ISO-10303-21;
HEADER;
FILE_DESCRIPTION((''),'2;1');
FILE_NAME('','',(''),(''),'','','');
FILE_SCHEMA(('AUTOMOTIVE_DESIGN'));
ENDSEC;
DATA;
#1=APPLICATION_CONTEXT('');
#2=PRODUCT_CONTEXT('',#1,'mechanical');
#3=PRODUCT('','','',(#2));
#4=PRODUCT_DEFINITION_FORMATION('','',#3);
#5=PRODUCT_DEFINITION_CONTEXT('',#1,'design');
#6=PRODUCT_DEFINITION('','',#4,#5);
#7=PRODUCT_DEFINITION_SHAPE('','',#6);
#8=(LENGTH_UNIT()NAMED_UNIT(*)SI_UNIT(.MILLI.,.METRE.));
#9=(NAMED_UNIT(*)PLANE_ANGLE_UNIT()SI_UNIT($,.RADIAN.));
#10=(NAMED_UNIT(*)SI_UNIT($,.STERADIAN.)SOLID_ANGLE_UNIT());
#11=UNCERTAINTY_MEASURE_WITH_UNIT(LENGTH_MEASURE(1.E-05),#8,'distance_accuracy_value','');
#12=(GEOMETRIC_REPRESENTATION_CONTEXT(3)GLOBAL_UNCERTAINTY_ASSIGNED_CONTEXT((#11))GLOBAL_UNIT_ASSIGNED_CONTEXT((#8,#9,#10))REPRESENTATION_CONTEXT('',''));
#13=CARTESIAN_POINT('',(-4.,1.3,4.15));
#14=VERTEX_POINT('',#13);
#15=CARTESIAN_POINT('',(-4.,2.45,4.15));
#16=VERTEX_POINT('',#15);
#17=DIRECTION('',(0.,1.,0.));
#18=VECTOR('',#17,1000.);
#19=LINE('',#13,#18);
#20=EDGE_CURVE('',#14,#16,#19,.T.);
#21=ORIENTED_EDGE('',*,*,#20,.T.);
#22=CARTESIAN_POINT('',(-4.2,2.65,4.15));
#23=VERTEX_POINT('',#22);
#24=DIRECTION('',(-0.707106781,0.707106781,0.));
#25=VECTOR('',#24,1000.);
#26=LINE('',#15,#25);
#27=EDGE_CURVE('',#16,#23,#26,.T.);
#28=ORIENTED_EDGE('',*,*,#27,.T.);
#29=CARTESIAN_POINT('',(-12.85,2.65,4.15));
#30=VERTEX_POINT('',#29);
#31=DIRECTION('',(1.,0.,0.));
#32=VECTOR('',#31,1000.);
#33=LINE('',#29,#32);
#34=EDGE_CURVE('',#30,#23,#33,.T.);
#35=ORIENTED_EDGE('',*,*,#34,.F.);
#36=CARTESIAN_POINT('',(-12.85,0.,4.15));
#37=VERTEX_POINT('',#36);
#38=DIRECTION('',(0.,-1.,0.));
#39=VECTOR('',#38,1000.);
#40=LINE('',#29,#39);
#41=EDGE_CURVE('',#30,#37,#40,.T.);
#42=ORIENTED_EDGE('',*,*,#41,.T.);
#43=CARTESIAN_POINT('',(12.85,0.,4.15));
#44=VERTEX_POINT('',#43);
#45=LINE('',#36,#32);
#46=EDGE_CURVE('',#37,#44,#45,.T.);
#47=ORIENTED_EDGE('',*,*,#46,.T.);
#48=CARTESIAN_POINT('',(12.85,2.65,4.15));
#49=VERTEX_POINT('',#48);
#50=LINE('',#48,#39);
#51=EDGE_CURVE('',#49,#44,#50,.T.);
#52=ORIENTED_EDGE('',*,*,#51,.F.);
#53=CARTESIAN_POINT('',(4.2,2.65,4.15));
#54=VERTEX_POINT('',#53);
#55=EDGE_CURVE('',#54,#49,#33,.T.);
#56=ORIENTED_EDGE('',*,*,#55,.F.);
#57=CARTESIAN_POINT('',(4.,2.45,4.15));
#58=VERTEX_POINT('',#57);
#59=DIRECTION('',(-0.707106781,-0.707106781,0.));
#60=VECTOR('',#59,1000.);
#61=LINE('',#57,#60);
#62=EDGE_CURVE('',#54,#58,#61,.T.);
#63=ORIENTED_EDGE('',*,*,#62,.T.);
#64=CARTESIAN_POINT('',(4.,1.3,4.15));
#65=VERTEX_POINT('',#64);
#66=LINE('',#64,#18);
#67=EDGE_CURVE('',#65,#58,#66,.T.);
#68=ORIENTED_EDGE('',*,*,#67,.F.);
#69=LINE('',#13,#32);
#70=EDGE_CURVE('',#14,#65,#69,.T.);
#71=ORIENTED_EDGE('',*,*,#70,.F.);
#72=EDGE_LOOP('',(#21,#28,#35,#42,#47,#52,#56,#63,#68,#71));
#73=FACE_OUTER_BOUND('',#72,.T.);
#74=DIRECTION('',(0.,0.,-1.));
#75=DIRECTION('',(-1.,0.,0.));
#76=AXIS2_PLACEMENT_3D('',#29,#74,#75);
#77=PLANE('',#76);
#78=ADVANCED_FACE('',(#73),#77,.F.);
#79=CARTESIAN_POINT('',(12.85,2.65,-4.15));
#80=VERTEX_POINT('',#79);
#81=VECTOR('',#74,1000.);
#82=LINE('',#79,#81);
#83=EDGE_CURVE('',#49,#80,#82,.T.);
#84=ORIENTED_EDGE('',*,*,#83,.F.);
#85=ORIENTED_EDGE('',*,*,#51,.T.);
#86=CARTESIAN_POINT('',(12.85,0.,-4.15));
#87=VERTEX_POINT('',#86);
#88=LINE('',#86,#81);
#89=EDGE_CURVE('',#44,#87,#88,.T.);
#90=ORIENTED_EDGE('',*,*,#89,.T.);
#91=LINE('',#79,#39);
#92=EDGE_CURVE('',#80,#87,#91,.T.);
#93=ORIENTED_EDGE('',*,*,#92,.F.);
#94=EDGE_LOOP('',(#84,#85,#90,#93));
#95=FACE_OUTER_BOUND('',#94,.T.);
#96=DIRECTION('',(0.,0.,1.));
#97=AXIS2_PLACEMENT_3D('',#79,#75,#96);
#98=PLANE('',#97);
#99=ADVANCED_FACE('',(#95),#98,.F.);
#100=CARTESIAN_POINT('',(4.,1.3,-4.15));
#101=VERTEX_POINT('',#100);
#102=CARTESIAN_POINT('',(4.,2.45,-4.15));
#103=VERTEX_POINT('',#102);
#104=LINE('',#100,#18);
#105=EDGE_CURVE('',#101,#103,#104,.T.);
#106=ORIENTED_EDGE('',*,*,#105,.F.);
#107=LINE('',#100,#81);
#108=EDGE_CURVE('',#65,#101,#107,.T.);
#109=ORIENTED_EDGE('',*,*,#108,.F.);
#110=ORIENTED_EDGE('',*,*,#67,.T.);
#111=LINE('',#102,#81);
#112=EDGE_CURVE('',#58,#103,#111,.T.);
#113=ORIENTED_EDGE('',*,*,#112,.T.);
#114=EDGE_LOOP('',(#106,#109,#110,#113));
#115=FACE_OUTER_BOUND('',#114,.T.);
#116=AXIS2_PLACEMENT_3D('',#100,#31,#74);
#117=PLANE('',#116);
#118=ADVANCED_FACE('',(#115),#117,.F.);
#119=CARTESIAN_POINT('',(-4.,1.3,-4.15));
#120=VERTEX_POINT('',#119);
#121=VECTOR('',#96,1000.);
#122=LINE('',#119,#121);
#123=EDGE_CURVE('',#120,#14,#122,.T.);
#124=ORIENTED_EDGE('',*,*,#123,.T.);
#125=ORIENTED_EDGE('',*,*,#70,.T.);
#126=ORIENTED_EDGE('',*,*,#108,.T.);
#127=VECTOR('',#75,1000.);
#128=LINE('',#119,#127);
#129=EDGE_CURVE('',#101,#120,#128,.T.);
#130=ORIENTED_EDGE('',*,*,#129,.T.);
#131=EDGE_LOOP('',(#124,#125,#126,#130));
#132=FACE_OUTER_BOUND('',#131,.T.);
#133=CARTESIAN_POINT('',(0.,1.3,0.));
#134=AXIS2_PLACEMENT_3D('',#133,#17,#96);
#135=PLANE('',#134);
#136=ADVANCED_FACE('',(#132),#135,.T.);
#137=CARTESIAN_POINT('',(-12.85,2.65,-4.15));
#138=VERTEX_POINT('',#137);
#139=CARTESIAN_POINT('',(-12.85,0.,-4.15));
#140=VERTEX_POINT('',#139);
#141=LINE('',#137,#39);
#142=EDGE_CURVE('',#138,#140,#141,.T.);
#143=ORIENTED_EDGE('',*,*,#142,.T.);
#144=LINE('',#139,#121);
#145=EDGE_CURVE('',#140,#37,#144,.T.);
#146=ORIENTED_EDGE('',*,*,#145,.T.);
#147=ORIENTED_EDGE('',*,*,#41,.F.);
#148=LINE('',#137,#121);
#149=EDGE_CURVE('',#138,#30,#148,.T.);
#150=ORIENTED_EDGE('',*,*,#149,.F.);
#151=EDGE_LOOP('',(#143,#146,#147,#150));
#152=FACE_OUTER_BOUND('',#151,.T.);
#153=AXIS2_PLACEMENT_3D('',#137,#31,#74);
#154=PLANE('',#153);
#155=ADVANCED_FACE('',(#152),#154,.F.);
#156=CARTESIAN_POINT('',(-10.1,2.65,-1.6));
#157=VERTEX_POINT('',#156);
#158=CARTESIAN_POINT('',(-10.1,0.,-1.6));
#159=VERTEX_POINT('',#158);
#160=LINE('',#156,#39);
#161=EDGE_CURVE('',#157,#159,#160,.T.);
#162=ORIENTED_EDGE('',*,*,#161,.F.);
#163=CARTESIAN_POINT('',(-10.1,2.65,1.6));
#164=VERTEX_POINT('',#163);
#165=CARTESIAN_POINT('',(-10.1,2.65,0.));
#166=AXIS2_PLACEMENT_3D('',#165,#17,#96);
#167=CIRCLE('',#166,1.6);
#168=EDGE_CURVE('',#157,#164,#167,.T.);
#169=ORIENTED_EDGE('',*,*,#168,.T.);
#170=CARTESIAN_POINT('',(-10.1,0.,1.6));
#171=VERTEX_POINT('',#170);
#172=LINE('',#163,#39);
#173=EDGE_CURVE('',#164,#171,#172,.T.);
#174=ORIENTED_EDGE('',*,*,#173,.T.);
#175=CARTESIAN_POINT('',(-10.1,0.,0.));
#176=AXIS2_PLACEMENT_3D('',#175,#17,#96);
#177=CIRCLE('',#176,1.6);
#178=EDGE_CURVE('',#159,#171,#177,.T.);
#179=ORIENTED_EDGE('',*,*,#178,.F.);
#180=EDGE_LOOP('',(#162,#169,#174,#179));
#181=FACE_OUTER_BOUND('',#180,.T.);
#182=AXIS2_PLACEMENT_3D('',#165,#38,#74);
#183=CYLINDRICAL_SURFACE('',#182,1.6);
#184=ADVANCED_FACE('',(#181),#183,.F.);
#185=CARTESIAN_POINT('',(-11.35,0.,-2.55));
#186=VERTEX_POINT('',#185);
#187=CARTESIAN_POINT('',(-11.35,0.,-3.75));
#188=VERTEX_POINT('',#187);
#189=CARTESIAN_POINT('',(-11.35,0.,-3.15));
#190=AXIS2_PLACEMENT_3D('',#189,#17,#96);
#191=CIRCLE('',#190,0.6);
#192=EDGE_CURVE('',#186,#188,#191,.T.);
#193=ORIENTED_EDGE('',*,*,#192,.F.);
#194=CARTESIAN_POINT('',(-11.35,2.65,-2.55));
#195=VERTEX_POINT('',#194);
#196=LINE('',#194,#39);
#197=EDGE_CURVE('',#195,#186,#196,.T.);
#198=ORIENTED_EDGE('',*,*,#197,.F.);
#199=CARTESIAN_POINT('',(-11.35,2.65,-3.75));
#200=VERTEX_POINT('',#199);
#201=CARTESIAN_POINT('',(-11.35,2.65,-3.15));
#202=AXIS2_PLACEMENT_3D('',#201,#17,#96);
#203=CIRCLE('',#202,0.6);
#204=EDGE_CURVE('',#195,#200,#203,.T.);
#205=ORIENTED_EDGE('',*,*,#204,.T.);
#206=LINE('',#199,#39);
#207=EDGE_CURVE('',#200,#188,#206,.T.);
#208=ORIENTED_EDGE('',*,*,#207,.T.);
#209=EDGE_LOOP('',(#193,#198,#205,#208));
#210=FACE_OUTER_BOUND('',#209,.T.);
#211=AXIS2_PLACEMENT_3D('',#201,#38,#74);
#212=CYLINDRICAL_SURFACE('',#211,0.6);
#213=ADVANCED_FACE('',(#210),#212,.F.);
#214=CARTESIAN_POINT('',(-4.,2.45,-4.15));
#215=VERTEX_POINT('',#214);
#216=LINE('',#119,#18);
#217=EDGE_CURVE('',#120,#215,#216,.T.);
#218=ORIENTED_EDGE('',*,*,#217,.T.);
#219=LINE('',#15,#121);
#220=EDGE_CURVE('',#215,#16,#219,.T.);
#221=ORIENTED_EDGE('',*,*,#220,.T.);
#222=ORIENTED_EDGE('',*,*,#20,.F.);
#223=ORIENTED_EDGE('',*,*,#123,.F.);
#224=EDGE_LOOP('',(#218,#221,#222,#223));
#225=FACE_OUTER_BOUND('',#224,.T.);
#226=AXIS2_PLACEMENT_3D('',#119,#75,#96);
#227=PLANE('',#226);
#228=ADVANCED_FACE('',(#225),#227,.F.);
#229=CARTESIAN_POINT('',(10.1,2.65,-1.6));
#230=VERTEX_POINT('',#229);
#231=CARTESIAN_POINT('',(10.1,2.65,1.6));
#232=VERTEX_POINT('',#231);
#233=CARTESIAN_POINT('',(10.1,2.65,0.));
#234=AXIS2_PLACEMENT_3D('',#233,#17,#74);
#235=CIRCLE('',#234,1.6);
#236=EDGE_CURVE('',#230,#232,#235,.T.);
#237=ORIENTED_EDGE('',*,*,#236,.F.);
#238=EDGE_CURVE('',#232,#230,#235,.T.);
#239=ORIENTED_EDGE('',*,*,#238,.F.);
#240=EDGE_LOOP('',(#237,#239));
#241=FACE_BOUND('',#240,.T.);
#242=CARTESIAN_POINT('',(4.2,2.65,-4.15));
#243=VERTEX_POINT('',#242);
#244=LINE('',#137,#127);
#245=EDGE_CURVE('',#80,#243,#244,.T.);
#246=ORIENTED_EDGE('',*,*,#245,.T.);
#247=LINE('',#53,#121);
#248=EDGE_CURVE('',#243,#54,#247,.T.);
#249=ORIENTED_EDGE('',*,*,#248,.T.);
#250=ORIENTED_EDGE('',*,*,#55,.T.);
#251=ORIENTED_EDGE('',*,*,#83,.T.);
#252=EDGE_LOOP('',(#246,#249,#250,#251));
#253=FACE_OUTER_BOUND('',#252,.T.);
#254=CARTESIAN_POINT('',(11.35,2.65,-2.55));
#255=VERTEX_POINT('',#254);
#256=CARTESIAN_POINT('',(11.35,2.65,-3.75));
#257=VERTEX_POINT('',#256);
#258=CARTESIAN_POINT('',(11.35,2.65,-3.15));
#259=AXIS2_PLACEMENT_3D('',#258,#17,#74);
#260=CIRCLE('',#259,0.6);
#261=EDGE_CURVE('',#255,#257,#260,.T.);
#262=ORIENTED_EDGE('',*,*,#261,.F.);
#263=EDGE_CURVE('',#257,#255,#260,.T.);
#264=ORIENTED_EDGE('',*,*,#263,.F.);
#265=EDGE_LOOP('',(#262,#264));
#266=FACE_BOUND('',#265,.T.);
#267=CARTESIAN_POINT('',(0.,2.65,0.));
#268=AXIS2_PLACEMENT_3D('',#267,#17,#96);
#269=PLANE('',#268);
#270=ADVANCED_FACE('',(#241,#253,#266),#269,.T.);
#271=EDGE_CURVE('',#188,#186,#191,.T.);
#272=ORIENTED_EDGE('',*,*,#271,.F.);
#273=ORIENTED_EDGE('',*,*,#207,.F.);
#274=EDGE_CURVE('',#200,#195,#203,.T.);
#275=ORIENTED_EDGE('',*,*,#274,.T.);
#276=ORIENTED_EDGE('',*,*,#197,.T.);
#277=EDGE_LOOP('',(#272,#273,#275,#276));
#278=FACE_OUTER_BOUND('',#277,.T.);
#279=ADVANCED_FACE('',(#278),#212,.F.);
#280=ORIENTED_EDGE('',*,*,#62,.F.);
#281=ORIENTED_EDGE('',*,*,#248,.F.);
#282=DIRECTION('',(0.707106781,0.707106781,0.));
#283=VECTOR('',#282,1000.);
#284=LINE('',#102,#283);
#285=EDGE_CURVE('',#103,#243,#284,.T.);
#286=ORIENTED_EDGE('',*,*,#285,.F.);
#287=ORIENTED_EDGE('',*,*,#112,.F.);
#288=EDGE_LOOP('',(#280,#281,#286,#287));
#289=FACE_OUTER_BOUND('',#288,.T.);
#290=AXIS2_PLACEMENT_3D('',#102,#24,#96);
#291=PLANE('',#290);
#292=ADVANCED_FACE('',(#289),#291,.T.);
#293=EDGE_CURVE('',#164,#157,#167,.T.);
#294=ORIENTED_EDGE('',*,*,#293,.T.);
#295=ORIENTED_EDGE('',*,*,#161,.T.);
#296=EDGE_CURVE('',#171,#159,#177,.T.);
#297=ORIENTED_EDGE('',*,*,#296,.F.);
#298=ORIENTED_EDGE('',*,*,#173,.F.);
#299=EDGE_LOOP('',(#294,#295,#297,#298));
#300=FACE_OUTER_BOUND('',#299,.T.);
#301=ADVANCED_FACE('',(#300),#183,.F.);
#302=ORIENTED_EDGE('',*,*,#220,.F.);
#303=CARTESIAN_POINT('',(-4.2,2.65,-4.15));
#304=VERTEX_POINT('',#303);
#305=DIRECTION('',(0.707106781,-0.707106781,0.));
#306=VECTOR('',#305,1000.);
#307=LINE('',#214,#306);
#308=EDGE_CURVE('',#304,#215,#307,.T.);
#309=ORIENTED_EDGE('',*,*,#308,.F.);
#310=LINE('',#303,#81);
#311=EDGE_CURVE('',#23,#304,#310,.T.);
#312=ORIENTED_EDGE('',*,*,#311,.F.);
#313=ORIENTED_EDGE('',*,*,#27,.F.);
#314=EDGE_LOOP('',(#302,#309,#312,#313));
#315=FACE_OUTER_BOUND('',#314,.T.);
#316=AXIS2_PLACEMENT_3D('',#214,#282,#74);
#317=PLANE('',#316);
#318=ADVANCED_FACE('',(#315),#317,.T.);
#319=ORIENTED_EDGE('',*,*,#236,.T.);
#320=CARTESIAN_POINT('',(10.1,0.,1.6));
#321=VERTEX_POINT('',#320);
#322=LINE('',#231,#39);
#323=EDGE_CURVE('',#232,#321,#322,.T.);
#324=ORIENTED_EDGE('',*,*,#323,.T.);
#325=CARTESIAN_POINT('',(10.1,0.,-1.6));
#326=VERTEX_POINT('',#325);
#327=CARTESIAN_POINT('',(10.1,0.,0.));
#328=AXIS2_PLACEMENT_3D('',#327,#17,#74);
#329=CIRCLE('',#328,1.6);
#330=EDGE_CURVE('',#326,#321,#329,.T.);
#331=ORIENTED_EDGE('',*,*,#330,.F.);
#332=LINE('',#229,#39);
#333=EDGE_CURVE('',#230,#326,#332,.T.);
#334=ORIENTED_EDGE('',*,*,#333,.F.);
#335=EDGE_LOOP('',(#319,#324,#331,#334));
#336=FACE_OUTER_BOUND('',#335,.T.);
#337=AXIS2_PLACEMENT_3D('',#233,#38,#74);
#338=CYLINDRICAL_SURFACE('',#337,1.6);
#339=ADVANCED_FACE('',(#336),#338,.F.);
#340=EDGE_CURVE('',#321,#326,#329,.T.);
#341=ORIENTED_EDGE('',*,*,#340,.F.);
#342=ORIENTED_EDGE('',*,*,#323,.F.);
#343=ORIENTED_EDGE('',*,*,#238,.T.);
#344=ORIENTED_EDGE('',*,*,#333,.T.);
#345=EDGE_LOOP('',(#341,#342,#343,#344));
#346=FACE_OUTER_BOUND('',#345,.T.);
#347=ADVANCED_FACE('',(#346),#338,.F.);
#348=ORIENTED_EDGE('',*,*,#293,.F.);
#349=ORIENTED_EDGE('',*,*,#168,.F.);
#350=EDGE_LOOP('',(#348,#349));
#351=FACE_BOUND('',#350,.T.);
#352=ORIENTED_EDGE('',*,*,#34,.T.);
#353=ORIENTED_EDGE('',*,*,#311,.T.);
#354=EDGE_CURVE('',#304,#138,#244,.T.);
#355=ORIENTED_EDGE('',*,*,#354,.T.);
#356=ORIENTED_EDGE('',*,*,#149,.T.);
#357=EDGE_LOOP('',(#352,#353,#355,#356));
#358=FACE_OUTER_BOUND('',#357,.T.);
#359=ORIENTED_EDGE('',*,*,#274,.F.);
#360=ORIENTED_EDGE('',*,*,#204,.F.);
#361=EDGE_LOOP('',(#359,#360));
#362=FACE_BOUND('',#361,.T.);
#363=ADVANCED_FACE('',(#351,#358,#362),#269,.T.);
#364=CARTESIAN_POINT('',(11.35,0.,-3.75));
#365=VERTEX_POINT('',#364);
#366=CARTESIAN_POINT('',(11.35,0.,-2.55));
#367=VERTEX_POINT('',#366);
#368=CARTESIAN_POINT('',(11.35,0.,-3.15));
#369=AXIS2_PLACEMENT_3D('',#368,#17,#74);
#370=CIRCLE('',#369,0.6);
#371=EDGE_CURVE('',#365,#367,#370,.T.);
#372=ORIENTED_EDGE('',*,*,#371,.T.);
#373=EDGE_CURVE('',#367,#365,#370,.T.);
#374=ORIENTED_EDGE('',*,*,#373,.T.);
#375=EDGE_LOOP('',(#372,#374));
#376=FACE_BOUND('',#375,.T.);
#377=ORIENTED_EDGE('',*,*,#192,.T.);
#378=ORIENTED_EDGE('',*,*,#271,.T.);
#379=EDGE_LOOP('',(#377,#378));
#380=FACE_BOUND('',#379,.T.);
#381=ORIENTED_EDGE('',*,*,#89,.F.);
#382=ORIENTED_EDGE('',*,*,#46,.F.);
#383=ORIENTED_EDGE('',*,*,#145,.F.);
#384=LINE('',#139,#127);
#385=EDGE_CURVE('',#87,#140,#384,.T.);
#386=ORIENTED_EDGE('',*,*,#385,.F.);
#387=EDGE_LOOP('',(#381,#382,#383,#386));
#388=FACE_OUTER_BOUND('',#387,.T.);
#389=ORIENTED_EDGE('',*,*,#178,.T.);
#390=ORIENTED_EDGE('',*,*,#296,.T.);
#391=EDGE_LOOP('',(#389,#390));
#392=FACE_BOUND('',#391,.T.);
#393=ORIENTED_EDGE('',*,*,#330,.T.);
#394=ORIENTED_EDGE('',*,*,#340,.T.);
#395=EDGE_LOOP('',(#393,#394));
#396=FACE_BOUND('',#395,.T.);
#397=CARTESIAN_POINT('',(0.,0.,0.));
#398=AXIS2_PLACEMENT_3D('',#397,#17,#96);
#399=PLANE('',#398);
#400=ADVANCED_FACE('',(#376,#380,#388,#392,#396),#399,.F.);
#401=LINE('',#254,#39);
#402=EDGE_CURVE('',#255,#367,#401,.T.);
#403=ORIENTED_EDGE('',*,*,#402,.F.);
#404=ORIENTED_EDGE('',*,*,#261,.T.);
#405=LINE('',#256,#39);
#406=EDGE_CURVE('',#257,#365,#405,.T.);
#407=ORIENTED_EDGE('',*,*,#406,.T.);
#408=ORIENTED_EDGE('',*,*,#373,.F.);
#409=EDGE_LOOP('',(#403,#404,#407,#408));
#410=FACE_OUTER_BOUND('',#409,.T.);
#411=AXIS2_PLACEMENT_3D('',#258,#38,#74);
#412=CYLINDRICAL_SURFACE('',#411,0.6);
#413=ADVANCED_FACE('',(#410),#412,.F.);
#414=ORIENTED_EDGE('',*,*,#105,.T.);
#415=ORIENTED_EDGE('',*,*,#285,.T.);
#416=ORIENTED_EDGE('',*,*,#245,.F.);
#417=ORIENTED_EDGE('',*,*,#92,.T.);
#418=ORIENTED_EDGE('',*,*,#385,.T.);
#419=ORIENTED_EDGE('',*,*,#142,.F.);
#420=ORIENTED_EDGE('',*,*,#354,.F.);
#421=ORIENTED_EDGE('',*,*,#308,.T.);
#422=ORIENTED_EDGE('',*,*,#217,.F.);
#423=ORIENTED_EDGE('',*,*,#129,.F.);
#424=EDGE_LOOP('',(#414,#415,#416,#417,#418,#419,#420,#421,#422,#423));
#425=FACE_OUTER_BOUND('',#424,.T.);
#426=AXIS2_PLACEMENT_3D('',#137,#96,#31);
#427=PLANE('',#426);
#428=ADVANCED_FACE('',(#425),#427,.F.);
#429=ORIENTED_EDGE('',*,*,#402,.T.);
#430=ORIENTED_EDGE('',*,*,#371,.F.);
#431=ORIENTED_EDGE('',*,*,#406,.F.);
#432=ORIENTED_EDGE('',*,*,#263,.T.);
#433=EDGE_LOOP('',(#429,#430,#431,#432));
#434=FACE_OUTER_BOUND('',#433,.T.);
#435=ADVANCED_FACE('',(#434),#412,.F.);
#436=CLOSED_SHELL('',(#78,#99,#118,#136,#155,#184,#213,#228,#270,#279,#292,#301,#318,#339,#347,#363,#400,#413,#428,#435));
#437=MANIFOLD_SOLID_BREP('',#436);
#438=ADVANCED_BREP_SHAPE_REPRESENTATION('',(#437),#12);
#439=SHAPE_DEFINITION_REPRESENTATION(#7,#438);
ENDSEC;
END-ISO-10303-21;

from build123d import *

# Parameters (mm, degrees)
SKETCH1_W           = 25.7
SKETCH1_H           = 8.3
SKETCH1_R           = 1.6
SKETCH1_R_2         = 0.6
BOSS_EXTRUDE1_DEPTH = 2.65
SKETCH2_W           = 8
SKETCH2_H           = 8.3
CUT_EXTRUDE1_DEPTH  = 1.35
CHAMFER1_SIZE       = 0.2


with BuildPart() as part:
    # Sketch1 → Boss-Extrude1 (new body)
    with BuildSketch(Plane(origin=(0, 0, 0), x_dir=(1, 0, 0), z_dir=(0, 1, 0))):
        Rectangle(SKETCH1_W, SKETCH1_H)
        with Locations(Location((-10.1, 0, 0), (0, 0, 270))):
            Circle(SKETCH1_R, mode=Mode.SUBTRACT)
        with Locations(Location((-11.35, 3.15, 0), (0, 0, 270))):
            Circle(SKETCH1_R_2, mode=Mode.SUBTRACT)
        with Locations(Location((11.35, 3.15, 0), (0, 0, 90))):
            Circle(SKETCH1_R_2, mode=Mode.SUBTRACT)
        with Locations(Location((10.1, 0, 0), (0, 0, 90))):
            Circle(SKETCH1_R, mode=Mode.SUBTRACT)
    extrude(amount=BOSS_EXTRUDE1_DEPTH)

    # Sketch2 → Cut-Extrude1 (cut)
    with BuildSketch(Plane(origin=(0, 2.65, 0), x_dir=(1, 0, 0), z_dir=(0, 1, 0))):
        Rectangle(SKETCH2_W, SKETCH2_H)
    extrude(amount=-CUT_EXTRUDE1_DEPTH, mode=Mode.SUBTRACT)

    # Chamfer1
    chamfer1_edges = [part.edges().sort_by_distance(p)[0] for p in [
        (4, 2.65, 0),
        (-4, 2.65, 0),
    ]]
    chamfer(chamfer1_edges, length=CHAMFER1_SIZE)


solid = part.part
